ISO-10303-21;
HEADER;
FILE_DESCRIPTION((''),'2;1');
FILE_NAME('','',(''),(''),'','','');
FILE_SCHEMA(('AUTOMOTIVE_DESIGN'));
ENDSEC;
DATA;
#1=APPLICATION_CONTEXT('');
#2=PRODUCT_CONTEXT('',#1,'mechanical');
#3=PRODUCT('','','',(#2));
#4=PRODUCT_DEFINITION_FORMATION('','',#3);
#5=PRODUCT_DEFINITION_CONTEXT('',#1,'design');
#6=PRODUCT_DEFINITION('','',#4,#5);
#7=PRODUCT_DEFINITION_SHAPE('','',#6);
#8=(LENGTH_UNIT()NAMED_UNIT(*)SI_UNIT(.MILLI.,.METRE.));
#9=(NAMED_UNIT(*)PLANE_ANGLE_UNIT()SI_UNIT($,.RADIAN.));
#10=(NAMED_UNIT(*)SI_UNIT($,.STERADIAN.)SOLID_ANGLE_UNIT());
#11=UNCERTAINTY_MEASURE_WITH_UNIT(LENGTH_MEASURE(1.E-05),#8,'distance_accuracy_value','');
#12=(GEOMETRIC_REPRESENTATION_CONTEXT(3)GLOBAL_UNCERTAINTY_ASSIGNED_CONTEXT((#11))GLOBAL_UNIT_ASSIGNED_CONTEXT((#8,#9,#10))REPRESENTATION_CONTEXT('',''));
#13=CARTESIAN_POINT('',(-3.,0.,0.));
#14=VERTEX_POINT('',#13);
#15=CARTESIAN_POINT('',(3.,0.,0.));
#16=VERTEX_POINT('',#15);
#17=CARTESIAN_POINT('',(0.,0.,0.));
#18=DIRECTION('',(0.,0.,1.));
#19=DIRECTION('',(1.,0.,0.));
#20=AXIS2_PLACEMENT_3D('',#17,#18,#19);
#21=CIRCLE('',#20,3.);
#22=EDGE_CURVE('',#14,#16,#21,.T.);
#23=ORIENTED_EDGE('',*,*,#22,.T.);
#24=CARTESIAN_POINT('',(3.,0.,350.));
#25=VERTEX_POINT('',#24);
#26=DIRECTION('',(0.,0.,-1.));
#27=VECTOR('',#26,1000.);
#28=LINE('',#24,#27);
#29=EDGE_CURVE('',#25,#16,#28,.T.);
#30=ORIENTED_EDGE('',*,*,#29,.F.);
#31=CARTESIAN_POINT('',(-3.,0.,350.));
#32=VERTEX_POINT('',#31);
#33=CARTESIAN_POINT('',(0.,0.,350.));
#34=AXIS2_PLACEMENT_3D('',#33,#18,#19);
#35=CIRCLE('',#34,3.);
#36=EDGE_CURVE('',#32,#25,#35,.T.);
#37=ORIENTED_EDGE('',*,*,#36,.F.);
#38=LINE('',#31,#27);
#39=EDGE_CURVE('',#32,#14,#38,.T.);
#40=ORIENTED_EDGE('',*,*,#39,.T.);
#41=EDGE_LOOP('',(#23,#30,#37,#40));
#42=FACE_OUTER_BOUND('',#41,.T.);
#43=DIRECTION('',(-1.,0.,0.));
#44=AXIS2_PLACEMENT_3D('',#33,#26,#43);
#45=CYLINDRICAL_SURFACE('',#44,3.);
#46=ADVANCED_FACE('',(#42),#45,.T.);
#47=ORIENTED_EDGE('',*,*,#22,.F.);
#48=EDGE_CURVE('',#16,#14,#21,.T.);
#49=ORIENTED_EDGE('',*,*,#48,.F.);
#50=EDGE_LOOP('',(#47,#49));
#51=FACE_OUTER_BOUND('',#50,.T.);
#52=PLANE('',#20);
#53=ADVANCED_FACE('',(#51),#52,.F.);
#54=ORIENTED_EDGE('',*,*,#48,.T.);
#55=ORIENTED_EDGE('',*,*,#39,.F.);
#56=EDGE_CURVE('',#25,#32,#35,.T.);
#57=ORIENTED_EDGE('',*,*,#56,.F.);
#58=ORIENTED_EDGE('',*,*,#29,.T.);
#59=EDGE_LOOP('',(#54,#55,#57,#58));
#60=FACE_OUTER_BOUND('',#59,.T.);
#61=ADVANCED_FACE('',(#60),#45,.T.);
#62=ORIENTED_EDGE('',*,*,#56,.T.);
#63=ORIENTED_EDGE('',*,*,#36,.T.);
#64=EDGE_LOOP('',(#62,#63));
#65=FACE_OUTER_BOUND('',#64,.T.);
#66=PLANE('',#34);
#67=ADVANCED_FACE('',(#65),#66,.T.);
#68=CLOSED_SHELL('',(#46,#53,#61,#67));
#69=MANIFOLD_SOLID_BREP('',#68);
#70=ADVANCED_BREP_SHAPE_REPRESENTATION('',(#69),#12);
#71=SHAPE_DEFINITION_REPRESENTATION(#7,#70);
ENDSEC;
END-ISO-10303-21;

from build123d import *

# Parameters (mm, degrees)
SKETCH1_R           = 3
BOSS_EXTRUDE1_DEPTH = 350


with BuildPart() as part:
    # Sketch1 → Boss-Extrude1 (new body)
    with BuildSketch(Plane.XY):
        Circle(SKETCH1_R)
    extrude(amount=BOSS_EXTRUDE1_DEPTH)


solid = part.part
